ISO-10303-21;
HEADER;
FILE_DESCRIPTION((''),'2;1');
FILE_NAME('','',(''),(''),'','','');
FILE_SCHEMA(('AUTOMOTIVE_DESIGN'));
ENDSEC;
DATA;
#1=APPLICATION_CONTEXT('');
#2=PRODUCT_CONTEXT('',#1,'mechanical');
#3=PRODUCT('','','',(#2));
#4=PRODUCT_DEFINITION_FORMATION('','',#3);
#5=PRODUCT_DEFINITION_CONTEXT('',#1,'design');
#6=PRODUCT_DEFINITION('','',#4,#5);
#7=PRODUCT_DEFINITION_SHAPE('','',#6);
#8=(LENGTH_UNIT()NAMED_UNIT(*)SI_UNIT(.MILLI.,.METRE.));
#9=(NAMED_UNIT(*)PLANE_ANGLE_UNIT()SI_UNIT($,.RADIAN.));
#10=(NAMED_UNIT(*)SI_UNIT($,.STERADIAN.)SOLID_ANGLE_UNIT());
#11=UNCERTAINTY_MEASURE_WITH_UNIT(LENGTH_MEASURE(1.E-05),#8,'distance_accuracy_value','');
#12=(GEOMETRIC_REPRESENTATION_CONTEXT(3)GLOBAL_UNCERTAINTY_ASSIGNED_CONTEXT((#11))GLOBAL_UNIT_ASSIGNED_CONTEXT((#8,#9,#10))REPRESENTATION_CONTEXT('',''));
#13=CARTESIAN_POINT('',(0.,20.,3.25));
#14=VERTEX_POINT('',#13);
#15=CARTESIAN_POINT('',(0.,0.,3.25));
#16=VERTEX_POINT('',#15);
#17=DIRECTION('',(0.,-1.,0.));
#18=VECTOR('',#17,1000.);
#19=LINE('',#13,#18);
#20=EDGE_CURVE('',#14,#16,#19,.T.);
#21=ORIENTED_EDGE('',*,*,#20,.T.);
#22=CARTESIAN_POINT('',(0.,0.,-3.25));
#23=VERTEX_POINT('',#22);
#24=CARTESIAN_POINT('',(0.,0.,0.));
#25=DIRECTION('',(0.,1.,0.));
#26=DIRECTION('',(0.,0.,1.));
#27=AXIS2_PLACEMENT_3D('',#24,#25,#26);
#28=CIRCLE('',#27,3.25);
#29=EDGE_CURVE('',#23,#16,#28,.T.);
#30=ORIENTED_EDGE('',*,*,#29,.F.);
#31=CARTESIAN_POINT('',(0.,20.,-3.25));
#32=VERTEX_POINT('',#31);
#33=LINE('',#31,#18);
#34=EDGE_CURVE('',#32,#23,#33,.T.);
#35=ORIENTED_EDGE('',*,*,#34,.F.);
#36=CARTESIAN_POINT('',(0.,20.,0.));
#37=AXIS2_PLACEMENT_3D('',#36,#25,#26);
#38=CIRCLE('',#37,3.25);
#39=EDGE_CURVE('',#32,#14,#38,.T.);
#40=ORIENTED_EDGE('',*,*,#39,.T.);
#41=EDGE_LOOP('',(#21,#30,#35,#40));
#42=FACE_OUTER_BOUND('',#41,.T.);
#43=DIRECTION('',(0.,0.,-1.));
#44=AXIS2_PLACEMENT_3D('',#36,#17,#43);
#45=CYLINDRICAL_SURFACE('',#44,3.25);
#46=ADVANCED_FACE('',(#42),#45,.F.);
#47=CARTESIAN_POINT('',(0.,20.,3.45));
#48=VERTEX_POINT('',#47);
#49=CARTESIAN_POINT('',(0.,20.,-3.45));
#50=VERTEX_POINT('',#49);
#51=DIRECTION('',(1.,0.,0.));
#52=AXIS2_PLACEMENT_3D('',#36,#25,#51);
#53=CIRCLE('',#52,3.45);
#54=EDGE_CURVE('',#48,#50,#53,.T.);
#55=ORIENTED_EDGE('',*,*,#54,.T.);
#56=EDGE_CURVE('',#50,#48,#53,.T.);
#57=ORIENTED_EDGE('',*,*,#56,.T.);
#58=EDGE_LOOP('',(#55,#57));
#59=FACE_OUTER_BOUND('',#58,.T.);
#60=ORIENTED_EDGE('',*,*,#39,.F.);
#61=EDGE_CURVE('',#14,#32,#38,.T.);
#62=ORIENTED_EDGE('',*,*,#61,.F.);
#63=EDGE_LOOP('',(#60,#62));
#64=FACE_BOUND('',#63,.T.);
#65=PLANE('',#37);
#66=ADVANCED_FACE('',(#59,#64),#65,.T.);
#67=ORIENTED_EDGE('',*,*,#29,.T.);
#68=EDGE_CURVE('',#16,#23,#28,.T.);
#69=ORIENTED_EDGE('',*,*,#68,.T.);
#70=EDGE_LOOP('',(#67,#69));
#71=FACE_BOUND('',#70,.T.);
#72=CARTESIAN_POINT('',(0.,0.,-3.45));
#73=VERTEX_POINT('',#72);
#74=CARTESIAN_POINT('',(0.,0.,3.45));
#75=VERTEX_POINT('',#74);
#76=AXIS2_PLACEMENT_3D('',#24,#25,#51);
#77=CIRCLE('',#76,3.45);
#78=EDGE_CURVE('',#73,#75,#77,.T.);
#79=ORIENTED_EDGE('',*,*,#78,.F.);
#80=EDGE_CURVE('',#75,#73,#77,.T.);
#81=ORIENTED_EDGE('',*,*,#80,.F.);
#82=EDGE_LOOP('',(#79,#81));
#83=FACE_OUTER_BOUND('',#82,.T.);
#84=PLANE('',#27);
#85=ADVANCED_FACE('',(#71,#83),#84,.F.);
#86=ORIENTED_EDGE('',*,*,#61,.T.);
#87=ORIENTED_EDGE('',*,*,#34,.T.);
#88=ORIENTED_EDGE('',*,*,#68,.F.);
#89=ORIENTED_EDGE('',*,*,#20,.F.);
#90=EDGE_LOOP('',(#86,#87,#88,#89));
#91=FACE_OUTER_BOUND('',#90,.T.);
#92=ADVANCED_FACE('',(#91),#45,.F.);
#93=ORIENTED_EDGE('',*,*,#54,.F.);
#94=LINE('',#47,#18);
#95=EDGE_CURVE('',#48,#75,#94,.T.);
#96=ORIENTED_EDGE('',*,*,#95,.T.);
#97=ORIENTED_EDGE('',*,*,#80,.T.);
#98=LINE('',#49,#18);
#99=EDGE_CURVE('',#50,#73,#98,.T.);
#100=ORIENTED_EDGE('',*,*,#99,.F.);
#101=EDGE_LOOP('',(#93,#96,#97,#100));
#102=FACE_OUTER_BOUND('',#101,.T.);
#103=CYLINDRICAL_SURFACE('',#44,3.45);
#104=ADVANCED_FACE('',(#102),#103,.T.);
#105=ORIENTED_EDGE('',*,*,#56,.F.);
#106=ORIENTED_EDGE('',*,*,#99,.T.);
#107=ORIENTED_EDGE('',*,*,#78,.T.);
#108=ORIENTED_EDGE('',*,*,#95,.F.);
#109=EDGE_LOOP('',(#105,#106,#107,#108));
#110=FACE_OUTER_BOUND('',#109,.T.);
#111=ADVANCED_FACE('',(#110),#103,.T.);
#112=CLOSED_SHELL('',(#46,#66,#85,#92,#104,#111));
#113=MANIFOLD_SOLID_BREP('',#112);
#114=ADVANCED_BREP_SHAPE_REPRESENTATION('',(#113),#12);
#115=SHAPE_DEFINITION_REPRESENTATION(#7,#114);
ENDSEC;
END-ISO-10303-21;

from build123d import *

# Parameters (mm, degrees)
SKETCH1_R           = 3.45
SKETCH1_R_2         = 3.25
EXTRUDE_THIN1_DEPTH = 20


with BuildPart() as part:
    # Sketch1 → Extrude-Thin1 (new body)
    with BuildSketch(Plane(origin=(0, 0, 0), x_dir=(1, 0, 0), z_dir=(0, 1, 0))):
        Circle(SKETCH1_R)
        Circle(SKETCH1_R_2, mode=Mode.SUBTRACT)
    extrude(amount=EXTRUDE_THIN1_DEPTH)


solid = part.part
